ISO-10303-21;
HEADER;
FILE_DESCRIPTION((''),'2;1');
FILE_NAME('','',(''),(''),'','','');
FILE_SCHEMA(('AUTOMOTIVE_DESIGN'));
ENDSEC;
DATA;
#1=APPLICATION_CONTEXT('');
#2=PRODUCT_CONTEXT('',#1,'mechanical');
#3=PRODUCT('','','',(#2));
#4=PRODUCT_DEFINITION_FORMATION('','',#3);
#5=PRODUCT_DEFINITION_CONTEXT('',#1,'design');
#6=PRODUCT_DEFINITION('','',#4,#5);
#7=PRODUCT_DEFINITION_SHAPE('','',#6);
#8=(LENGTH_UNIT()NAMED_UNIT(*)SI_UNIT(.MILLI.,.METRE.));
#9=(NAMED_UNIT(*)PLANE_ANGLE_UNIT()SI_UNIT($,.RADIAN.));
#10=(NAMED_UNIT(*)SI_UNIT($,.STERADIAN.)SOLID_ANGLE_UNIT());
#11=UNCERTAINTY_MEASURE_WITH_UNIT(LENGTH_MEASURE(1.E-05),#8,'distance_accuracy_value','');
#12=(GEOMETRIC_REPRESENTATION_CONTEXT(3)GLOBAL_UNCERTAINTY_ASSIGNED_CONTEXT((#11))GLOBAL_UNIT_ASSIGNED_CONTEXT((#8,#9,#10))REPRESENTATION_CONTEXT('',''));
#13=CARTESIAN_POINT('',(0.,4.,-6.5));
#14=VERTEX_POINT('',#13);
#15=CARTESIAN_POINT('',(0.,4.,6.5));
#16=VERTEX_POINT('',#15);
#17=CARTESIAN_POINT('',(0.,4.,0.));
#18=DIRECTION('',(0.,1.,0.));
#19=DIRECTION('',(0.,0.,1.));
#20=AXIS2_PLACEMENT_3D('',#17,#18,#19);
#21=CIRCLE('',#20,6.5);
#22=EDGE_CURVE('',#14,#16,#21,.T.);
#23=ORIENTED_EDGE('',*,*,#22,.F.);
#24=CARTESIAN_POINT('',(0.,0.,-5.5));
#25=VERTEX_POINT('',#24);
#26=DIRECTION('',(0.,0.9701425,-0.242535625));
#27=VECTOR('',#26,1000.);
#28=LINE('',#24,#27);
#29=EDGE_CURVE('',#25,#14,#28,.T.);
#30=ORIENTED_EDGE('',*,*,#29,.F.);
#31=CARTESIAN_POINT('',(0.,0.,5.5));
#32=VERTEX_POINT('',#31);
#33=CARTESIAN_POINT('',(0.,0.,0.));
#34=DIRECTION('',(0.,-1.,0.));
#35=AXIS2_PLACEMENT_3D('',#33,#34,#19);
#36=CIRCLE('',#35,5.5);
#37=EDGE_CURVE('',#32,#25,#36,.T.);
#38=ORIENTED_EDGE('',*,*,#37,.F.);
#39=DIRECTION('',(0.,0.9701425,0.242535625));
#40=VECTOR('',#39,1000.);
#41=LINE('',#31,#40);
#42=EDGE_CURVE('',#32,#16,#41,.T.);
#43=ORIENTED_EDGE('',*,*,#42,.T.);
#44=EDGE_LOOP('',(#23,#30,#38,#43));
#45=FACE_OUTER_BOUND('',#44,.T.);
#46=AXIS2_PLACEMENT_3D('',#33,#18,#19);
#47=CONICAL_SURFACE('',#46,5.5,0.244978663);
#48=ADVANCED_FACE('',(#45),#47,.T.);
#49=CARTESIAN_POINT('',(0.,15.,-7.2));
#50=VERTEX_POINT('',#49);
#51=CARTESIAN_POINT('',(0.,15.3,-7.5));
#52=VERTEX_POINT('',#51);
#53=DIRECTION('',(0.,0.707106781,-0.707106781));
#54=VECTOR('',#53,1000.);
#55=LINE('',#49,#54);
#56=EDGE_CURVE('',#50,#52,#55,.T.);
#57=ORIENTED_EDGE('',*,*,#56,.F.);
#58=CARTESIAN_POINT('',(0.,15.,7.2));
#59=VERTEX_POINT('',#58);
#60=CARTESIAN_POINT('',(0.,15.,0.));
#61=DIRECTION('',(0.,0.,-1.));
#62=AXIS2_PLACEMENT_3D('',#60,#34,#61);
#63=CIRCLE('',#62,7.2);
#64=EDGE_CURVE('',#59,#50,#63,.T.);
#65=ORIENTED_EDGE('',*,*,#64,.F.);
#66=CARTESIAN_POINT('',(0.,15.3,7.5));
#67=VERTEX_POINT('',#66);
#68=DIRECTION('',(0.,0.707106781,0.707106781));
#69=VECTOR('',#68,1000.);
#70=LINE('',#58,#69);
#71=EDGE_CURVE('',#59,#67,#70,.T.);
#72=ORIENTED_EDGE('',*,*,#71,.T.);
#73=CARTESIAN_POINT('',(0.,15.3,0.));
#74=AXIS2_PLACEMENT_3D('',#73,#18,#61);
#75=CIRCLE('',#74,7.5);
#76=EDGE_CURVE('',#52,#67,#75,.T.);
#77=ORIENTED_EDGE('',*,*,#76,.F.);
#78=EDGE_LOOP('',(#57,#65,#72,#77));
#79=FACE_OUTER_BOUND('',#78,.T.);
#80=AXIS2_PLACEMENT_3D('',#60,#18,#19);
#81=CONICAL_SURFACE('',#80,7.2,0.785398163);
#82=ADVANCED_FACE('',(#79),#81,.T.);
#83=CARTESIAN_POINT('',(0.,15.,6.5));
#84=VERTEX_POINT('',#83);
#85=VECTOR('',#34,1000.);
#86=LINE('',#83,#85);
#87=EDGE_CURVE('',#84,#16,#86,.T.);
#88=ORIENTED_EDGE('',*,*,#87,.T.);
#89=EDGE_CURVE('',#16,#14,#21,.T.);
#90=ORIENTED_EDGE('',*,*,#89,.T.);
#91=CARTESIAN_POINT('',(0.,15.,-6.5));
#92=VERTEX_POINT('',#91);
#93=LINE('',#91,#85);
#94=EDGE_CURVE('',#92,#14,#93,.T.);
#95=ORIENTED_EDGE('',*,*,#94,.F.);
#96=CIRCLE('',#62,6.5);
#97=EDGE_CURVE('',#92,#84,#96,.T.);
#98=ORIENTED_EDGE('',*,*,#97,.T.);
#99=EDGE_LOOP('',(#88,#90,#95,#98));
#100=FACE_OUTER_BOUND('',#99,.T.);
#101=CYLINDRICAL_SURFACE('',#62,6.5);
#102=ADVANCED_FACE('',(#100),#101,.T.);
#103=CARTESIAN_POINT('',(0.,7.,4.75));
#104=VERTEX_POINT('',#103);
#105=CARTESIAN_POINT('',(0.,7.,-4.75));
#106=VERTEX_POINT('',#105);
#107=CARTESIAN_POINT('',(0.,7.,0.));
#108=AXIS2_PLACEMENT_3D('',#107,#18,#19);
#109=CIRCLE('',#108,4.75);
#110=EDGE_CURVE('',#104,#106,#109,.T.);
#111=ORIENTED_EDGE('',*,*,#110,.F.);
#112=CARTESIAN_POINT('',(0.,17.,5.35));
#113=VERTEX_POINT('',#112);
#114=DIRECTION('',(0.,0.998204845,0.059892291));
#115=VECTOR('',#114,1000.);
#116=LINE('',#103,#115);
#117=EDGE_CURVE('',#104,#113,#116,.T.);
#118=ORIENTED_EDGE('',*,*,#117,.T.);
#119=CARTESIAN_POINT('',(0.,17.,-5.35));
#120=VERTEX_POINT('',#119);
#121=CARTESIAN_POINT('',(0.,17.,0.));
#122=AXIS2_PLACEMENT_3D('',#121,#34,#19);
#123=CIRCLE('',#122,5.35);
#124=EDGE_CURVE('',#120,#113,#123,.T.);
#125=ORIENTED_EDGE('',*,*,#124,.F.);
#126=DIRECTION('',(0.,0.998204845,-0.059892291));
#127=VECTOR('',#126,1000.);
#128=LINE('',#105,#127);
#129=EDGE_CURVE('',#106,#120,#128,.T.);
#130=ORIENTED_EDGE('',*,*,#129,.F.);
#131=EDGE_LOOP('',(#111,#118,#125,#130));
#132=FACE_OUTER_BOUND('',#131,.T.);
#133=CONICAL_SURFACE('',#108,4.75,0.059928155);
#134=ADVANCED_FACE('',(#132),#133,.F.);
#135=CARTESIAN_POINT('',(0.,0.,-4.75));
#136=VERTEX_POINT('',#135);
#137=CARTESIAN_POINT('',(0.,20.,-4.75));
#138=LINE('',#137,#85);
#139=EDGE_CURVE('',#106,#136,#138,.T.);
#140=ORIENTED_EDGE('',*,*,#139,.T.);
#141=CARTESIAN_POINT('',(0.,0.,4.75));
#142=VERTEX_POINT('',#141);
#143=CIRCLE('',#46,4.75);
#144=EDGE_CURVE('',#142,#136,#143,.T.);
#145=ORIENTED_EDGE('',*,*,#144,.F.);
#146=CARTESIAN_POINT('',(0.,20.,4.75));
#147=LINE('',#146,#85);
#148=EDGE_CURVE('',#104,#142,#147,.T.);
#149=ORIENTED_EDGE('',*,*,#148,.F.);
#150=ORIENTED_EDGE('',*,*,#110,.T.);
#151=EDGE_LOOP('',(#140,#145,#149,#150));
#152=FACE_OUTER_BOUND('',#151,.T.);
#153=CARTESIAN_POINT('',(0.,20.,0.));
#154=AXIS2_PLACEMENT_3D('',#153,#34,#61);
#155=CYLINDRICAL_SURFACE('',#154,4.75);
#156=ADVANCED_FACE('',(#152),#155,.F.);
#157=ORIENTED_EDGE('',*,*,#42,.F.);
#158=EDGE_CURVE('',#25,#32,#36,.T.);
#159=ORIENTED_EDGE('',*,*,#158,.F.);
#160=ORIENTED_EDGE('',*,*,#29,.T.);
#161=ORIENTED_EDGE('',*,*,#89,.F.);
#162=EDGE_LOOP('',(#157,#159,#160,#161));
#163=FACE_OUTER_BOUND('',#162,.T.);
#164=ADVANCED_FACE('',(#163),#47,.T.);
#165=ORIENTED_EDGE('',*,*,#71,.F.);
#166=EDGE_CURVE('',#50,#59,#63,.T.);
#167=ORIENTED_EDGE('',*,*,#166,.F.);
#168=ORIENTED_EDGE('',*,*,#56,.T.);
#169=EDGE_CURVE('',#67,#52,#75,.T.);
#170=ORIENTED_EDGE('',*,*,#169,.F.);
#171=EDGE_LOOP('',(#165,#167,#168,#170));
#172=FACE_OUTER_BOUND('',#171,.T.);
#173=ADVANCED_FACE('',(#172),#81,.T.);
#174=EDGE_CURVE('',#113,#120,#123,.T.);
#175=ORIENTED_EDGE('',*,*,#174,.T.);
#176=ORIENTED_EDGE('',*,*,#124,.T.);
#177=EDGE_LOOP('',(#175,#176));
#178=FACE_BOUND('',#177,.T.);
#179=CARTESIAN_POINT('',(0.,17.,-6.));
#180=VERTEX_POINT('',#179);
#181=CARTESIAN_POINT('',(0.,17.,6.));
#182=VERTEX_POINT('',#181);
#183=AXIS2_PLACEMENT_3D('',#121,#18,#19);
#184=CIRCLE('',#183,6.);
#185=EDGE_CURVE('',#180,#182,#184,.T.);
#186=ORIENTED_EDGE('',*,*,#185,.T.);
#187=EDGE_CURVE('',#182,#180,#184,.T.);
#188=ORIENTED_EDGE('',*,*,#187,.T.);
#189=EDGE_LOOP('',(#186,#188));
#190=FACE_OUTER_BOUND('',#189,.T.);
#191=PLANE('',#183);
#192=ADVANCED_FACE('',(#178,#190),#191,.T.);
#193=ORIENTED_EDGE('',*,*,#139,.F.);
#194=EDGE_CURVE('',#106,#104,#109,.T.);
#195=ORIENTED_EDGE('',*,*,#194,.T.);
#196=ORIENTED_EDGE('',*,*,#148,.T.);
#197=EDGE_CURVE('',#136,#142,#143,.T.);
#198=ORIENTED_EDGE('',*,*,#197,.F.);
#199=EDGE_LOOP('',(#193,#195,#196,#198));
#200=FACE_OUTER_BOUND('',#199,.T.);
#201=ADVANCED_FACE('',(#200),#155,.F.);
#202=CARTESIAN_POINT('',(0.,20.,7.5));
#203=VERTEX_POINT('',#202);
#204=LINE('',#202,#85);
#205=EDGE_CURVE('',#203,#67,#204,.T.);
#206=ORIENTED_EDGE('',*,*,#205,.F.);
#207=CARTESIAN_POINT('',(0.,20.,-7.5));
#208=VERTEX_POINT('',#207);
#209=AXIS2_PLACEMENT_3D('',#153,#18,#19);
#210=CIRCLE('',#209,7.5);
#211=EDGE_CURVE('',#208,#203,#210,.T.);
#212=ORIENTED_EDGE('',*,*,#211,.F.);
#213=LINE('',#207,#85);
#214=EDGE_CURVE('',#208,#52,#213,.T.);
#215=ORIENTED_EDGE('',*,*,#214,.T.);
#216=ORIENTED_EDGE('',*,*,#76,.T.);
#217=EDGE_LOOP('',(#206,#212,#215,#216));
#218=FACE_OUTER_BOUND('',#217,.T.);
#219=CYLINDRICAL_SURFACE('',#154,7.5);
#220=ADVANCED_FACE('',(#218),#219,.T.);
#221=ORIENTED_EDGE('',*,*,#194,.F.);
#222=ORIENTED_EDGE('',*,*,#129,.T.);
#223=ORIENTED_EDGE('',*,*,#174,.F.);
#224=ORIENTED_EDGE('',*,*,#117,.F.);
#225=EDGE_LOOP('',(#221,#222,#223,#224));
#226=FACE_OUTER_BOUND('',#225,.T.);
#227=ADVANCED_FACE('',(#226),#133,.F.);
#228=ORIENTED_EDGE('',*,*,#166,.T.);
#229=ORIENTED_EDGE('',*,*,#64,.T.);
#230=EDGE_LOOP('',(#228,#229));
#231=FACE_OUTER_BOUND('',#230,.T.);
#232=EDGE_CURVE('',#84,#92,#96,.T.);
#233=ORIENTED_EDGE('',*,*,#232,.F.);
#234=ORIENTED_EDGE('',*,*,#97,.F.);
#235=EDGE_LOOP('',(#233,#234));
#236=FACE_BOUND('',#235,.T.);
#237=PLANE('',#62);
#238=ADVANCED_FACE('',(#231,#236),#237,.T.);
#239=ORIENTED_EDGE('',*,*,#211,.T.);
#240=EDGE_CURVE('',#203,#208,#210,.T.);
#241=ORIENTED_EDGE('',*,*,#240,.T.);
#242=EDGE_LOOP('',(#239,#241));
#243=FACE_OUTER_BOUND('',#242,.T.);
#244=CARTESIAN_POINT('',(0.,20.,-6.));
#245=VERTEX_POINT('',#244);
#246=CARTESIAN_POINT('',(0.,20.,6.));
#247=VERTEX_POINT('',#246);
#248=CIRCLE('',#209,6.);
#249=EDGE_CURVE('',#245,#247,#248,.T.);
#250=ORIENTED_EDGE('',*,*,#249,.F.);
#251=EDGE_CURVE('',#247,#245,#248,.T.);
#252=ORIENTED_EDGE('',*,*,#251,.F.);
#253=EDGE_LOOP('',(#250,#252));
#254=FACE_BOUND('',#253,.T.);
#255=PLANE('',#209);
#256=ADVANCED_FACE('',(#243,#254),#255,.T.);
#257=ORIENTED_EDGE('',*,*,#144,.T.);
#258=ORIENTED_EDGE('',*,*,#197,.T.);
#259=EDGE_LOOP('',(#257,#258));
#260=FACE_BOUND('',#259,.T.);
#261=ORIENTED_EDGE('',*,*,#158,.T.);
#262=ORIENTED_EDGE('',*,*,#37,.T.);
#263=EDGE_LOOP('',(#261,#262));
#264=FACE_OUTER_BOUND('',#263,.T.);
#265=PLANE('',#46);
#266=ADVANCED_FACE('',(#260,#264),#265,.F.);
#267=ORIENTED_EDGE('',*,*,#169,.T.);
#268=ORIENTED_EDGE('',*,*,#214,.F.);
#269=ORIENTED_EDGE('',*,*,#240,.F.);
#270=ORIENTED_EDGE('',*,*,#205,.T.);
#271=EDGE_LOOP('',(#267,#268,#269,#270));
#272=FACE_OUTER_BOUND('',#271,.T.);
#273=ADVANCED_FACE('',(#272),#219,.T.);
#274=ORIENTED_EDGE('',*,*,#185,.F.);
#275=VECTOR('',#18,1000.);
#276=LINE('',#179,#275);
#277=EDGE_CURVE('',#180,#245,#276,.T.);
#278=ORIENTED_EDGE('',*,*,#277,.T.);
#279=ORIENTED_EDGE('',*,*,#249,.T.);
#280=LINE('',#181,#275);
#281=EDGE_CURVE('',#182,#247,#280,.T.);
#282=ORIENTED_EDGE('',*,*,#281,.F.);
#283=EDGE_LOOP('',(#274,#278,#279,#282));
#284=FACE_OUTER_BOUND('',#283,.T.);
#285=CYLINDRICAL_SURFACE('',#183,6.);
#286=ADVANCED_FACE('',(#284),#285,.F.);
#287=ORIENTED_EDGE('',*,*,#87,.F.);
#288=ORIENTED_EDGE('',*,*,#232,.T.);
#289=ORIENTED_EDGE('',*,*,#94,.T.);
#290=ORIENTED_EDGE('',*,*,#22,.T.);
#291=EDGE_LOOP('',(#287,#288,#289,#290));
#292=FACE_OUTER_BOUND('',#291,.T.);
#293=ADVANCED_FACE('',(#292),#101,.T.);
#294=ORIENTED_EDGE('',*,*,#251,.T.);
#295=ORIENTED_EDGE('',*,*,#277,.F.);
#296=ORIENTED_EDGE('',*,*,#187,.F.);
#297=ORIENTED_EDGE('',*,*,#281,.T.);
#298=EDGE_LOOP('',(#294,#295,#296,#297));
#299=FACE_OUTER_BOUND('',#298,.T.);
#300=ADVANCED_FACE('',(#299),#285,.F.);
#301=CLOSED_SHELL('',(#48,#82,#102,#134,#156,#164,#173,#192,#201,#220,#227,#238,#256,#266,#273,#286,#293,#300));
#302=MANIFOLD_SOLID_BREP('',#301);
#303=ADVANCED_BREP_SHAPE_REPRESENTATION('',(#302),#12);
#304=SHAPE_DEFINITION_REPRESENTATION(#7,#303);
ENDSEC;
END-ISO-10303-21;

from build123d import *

# Parameters (mm, degrees)
SKETCH1_R           = 7.5
SKETCH1_R_2         = 4.75
BOSS_EXTRUDE1_DEPTH = 20
SKETCH2_R           = 6
CUT_EXTRUDE1_DEPTH  = 3
SKETCH3_OUTSIDE_W   = 22.83
SKETCH3_OUTSIDE_H   = 22.83
SKETCH3_OUTSIDE_R   = 6.5
CUT_EXTRUDE2_DEPTH  = 15
CHAMFER1_SIZE       = 0.6
CHAMFER1_SIZE2      = 10
CHAMFER2_SIZE       = 0.3
CHAMFER3_SIZE       = 4
CHAMFER3_SIZE2      = 1


with BuildPart() as part:
    # Sketch1 → Boss-Extrude1 (new body)
    with BuildSketch(Plane(origin=(0, 0, 0), x_dir=(1, 0, 0), z_dir=(0, 1, 0))):
        with Locations(Location((0, 0, 0), (0, 0, 270))):
            Circle(SKETCH1_R)
        with Locations(Location((0, 0, 0), (0, 0, 270))):
            Circle(SKETCH1_R_2, mode=Mode.SUBTRACT)
    extrude(amount=BOSS_EXTRUDE1_DEPTH)

    # Sketch2 → Cut-Extrude1 (cut)
    with BuildSketch(Plane(origin=(0, 20, 0), x_dir=(1, 0, 0), z_dir=(0, 1, 0))):
        with Locations(Location((0, 0, 0), (0, 0, 270))):
            Circle(SKETCH2_R)
    extrude(amount=-CUT_EXTRUDE1_DEPTH, mode=Mode.SUBTRACT)

    # Sketch3 outside → Cut-Extrude2 (cut)
    with BuildSketch(Plane.XZ):
        Rectangle(SKETCH3_OUTSIDE_W, SKETCH3_OUTSIDE_H)
        with Locations(Location((0, 0, 0), (0, 0, 270))):
            Circle(SKETCH3_OUTSIDE_R, mode=Mode.SUBTRACT)
    extrude(amount=-CUT_EXTRUDE2_DEPTH, mode=Mode.SUBTRACT)

    # Chamfer1
    chamfer1_edges = [part.edges().sort_by_distance(p)[0] for p in [
        (0, 17, -4.75),
    ]]
    chamfer1_side = [part.faces().sort_by_distance(p)[0] for p in [
        (0, 17, -5.830294373),
    ]]
    chamfer(chamfer1_edges, length=CHAMFER1_SIZE, length2=CHAMFER1_SIZE2, reference=chamfer1_side[0])

    # Chamfer2
    chamfer2_edges = [part.edges().sort_by_distance(p)[0] for p in [
        (0, 15, -7.5),
    ]]
    chamfer(chamfer2_edges, length=CHAMFER2_SIZE)

    # Chamfer3
    chamfer3_edges = [part.edges().sort_by_distance(p)[0] for p in [
        (0, 0, 6.5),
    ]]
    chamfer3_side = [part.faces().sort_by_distance(p)[0] for p in [
        (0, 7.5, 6.5),
    ]]
    chamfer(chamfer3_edges, length=CHAMFER3_SIZE, length2=CHAMFER3_SIZE2, reference=chamfer3_side[0])


solid = part.part
